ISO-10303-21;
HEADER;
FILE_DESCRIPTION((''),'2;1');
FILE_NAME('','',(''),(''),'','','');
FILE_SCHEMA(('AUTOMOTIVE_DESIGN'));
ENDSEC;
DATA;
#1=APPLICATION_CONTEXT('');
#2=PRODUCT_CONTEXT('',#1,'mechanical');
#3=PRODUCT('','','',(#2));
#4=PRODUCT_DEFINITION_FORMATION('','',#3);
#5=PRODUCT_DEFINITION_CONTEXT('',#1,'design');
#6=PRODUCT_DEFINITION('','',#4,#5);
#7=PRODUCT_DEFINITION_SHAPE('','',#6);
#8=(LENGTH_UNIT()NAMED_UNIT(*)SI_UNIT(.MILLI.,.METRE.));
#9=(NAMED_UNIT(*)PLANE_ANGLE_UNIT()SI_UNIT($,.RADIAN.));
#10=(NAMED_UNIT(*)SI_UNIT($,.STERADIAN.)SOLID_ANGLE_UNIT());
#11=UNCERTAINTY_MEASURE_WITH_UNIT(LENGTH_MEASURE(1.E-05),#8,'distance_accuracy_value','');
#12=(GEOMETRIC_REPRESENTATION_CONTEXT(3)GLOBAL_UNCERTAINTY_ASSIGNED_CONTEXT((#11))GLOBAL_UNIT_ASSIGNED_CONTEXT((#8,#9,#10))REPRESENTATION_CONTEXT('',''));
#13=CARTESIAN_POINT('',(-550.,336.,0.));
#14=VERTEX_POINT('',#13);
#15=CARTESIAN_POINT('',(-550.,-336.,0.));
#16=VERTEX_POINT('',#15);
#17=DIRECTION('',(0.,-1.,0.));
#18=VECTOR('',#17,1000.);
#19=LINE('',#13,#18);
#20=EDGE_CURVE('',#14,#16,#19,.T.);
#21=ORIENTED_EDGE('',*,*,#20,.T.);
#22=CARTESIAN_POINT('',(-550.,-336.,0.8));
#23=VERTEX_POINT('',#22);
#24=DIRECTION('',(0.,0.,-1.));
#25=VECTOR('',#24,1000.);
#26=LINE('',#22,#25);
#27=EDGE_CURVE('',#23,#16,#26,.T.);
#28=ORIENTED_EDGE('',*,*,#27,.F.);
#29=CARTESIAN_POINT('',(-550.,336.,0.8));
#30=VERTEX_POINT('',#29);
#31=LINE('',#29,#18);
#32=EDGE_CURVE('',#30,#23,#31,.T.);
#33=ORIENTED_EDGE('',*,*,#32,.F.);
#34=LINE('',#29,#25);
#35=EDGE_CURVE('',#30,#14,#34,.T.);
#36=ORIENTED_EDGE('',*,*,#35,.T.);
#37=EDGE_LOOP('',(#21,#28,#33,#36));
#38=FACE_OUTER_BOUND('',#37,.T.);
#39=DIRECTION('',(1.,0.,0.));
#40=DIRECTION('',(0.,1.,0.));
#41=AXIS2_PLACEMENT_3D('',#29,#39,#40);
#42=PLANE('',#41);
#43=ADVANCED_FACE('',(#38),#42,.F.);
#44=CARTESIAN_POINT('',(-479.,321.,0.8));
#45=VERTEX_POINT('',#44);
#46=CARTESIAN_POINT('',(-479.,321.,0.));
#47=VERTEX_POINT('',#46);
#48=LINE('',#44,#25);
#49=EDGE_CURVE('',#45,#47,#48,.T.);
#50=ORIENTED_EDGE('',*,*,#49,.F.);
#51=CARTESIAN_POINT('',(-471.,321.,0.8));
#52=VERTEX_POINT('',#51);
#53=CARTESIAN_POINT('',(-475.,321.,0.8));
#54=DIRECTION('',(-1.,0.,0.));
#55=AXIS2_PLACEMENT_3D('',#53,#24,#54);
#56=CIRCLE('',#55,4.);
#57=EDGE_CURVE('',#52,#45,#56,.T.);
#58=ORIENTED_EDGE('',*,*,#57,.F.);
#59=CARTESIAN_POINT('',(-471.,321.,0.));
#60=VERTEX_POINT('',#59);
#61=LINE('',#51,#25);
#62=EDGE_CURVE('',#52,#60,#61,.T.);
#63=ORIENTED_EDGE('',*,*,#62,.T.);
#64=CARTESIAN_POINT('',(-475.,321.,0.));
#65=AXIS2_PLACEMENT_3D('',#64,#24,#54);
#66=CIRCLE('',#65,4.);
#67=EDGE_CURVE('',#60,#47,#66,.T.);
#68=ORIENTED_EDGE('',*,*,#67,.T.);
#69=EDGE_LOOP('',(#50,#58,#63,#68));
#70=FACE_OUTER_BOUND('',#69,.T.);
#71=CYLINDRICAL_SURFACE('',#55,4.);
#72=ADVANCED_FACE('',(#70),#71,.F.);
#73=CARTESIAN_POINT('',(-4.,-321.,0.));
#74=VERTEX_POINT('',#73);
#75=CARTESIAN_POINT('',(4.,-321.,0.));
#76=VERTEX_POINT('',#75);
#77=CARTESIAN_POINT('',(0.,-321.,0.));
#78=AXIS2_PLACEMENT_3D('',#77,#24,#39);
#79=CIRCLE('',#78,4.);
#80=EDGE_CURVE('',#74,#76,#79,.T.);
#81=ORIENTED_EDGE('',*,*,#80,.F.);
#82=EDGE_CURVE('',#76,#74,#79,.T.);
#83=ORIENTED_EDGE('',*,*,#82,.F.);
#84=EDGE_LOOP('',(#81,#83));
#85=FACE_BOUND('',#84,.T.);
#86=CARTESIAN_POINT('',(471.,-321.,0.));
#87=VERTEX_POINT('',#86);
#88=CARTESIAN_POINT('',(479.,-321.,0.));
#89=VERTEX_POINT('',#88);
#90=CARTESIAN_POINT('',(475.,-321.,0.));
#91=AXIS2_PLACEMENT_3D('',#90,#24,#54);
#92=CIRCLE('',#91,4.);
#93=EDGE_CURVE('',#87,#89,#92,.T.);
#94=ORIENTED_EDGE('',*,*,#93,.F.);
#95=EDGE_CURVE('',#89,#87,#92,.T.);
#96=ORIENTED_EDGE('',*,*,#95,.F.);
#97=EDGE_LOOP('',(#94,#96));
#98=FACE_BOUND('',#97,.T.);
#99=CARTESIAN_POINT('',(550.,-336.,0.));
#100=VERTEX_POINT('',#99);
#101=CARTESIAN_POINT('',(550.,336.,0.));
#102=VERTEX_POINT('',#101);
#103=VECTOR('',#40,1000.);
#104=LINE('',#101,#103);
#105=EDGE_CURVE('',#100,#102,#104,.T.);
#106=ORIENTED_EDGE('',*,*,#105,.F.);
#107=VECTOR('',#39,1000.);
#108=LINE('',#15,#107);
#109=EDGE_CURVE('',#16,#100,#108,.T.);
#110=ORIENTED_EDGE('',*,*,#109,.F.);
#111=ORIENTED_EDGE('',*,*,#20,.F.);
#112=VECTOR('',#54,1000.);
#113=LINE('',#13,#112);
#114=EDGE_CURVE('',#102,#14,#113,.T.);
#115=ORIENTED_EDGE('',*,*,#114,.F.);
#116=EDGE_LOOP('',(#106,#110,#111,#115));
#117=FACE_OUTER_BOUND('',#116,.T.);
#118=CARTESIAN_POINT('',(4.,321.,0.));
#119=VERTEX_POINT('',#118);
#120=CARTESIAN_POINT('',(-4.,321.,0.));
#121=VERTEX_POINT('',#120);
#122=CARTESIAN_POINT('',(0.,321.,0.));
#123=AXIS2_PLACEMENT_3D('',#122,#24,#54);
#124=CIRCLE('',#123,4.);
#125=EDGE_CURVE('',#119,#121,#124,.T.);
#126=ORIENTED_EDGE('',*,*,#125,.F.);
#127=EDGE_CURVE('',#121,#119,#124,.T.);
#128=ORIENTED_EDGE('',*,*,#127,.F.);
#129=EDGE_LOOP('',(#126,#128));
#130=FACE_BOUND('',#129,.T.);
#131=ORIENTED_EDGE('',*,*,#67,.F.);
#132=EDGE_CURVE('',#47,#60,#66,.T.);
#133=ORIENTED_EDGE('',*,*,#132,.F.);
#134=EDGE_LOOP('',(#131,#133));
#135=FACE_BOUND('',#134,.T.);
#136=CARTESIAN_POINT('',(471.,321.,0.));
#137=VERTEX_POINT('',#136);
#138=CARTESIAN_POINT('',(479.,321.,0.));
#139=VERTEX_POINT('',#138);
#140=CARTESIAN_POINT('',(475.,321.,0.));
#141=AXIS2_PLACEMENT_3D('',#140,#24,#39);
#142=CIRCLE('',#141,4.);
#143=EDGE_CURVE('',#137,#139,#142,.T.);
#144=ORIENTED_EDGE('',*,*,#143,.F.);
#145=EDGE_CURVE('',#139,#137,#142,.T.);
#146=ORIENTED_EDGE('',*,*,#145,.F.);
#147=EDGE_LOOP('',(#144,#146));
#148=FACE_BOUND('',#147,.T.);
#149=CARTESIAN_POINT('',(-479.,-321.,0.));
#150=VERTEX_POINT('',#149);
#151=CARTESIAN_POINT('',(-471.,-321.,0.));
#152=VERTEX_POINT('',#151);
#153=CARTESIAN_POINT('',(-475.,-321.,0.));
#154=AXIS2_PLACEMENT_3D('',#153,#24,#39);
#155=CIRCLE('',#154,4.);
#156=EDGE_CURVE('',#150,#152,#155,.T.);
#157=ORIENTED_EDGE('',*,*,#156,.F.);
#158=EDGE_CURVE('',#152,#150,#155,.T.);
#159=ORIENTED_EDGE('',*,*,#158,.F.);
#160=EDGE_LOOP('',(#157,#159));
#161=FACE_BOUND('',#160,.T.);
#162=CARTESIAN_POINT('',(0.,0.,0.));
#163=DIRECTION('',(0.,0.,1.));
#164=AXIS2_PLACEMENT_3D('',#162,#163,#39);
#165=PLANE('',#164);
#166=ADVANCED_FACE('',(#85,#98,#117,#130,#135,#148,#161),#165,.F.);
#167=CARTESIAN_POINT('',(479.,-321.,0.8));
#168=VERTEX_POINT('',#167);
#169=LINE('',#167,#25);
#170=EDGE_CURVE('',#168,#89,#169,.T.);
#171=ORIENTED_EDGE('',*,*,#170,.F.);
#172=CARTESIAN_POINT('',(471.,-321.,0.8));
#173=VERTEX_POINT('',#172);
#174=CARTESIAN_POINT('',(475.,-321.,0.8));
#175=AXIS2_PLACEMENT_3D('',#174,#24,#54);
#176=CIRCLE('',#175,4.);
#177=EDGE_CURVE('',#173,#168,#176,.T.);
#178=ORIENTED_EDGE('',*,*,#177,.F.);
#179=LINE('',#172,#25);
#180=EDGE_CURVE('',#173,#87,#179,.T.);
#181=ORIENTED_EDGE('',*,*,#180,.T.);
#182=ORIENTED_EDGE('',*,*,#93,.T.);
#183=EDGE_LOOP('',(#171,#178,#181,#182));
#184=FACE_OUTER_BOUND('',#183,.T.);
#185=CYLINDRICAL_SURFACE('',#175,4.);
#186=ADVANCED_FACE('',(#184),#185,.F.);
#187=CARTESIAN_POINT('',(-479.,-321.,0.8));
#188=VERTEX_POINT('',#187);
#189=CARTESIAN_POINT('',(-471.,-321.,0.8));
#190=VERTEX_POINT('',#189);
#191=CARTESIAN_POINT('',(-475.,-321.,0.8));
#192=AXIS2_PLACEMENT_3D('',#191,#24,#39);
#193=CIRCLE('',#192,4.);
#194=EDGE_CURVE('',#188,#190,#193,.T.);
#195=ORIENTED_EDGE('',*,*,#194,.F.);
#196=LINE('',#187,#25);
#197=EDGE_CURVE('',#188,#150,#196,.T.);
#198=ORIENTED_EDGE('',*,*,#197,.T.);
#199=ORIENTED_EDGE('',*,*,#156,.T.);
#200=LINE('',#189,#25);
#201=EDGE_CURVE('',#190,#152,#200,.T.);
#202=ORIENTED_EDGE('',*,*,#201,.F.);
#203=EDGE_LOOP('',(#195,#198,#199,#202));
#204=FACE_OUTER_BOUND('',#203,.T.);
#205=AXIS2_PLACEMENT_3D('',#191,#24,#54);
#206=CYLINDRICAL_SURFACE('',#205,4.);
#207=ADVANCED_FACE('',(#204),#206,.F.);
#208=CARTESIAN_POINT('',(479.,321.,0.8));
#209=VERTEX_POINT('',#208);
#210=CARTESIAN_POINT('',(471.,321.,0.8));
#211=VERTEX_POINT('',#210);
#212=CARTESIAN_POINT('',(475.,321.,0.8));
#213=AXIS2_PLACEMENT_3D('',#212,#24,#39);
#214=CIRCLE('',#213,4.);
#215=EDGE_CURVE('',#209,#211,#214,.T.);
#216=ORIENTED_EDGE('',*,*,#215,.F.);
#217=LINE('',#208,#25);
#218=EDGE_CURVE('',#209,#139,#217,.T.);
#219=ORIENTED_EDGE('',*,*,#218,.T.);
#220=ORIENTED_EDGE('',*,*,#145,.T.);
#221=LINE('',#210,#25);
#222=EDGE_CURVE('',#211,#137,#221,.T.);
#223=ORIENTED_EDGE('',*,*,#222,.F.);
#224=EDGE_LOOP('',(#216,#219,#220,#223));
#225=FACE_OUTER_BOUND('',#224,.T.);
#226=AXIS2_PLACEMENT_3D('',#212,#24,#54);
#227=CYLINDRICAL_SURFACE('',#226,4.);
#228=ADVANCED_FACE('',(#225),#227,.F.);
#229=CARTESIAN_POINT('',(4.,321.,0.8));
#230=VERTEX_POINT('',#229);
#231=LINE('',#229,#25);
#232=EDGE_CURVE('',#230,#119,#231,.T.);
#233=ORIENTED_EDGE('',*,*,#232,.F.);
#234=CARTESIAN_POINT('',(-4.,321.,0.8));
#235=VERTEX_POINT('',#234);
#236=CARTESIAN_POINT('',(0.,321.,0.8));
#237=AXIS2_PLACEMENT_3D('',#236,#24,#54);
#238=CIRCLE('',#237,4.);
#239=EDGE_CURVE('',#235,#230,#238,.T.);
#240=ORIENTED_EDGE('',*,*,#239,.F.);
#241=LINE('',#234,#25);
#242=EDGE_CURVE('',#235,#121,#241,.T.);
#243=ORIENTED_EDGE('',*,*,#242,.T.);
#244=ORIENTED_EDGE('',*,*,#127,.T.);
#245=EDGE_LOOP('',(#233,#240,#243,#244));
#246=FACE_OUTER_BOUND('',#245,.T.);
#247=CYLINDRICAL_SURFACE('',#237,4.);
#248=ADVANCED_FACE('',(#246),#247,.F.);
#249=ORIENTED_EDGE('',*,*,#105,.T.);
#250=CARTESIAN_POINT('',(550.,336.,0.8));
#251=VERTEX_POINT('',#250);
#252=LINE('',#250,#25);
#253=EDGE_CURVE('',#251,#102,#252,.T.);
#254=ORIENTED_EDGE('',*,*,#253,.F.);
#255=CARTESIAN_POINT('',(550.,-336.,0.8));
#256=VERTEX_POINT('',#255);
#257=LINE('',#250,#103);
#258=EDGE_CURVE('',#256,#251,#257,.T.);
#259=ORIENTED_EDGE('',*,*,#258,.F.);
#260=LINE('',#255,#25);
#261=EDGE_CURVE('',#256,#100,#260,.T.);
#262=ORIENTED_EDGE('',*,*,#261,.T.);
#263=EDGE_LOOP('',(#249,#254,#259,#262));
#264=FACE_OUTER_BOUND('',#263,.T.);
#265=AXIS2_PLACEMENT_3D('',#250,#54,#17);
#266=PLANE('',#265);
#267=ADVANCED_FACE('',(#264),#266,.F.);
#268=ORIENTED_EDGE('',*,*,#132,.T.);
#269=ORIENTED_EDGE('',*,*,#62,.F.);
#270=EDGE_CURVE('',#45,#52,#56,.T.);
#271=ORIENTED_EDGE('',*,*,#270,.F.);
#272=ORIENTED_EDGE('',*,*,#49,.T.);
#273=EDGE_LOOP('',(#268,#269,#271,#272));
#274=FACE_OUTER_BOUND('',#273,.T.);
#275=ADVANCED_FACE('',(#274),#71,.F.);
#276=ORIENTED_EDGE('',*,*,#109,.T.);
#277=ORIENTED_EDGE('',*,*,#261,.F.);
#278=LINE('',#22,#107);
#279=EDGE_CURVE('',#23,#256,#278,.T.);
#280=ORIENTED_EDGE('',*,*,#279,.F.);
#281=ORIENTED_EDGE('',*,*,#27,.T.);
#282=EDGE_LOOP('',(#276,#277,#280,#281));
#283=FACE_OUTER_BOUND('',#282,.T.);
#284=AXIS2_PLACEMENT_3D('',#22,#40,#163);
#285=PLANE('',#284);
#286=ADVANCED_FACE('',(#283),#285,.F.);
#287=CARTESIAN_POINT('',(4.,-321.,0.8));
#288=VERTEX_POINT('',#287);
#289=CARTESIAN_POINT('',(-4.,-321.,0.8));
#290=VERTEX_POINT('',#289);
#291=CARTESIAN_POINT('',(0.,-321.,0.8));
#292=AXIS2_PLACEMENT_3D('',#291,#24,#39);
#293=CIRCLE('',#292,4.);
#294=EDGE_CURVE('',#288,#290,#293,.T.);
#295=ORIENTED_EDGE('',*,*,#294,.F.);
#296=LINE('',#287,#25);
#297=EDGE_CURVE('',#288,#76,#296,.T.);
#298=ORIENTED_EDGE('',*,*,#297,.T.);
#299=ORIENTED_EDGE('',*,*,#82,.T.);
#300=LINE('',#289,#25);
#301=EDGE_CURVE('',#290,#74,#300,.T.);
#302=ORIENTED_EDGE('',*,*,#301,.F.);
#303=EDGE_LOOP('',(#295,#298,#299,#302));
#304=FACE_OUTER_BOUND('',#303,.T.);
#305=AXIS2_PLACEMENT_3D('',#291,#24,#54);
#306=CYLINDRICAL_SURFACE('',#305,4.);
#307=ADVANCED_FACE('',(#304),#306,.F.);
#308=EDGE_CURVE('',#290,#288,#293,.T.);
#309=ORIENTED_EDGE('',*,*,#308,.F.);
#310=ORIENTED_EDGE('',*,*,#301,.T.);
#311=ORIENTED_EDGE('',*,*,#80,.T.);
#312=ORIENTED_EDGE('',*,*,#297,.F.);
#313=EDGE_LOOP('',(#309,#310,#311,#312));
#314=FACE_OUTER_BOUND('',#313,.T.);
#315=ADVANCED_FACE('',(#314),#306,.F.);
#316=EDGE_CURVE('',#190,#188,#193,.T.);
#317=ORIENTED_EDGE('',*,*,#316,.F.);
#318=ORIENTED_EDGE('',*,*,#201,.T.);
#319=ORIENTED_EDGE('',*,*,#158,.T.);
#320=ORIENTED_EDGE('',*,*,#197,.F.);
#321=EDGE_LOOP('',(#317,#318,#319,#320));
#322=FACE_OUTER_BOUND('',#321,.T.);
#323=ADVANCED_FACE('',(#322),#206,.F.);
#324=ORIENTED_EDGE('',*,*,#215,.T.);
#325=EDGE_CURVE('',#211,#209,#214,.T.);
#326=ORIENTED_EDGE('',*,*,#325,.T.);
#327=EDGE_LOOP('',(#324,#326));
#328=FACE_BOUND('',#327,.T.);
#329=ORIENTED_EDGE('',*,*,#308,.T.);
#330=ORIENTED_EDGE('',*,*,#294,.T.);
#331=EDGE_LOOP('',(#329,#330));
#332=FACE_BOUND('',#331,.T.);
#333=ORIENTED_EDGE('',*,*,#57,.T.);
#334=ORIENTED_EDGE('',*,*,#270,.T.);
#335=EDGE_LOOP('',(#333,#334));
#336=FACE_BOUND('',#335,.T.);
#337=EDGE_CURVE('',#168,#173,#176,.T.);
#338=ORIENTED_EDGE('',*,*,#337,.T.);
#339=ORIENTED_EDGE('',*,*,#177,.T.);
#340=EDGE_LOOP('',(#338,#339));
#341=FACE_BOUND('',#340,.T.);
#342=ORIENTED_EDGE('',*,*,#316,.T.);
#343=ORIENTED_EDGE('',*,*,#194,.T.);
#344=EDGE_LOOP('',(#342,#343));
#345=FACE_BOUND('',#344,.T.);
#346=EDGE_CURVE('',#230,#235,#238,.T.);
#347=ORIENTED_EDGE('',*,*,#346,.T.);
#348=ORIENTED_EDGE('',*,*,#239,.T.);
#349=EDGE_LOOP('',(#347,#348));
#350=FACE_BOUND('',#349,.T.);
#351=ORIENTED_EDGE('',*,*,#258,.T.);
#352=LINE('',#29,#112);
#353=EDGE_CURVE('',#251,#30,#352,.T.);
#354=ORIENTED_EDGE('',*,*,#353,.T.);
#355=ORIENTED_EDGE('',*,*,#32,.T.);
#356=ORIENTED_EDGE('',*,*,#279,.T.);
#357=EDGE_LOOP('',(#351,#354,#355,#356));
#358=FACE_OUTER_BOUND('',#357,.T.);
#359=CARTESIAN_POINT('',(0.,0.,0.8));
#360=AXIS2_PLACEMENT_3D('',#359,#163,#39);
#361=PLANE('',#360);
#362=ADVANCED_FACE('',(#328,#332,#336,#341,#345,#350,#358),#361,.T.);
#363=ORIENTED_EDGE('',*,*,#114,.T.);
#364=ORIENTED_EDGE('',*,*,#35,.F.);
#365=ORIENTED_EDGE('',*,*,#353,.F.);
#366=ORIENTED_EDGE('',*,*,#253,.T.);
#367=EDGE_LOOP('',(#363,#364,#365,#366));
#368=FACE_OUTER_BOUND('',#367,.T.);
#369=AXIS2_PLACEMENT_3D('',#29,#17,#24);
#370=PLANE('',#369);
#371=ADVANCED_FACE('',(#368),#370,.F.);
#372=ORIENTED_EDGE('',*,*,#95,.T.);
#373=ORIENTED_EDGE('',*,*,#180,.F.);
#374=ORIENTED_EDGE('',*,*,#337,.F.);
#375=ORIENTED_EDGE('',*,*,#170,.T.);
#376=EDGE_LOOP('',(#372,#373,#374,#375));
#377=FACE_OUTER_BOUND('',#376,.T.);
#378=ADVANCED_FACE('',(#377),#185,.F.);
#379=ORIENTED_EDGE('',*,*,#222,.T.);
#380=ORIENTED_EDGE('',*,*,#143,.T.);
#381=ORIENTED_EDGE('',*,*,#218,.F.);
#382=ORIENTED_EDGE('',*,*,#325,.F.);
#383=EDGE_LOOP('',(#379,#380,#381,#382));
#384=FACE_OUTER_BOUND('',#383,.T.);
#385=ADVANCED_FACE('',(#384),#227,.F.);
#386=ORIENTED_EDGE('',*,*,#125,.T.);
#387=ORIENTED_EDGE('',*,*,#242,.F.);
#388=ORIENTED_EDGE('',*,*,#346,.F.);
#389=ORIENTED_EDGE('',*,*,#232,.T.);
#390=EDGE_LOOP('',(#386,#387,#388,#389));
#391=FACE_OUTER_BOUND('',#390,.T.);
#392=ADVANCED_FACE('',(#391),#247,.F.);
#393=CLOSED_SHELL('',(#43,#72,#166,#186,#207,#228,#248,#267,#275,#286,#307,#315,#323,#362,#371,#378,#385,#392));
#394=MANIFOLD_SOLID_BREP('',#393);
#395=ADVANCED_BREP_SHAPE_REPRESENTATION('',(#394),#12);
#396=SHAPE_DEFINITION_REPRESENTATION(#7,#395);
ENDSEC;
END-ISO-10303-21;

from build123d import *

# Parameters (mm, degrees)
SKETCH_1_W          = 1100
SKETCH_1_H          = 672
EXTRUDE_1_DEPTH     = 0.8
SKETCH_2_R          = 4
CUT_EXTRUDE_1_DEPTH = 0.8


with BuildPart() as part:
    # 草图1 → 凸台-拉伸1 (new body)
    with BuildSketch(Plane.XY):
        Rectangle(SKETCH_1_W, SKETCH_1_H)
    extrude(amount=EXTRUDE_1_DEPTH)

    # 草图2 → 切除-拉伸1 (cut)
    with BuildSketch(Plane(origin=(0, 0, 0), x_dir=(-1, 0, 0), z_dir=(0, 0, -1))):
        with Locations((0, 321)):
            Circle(SKETCH_2_R)
        with Locations((475, 321)):
            Circle(SKETCH_2_R)
        with Locations(Location((-475, 321, 0), (0, 0, 180))):
            Circle(SKETCH_2_R)
        with Locations((-475, -321)):
            Circle(SKETCH_2_R)
        with Locations(Location((475, -321, 0), (0, 0, 180))):
            Circle(SKETCH_2_R)
        with Locations(Location((0, -321, 0), (0, 0, 180))):
            Circle(SKETCH_2_R)
    extrude(amount=-CUT_EXTRUDE_1_DEPTH, mode=Mode.SUBTRACT)


solid = part.part
